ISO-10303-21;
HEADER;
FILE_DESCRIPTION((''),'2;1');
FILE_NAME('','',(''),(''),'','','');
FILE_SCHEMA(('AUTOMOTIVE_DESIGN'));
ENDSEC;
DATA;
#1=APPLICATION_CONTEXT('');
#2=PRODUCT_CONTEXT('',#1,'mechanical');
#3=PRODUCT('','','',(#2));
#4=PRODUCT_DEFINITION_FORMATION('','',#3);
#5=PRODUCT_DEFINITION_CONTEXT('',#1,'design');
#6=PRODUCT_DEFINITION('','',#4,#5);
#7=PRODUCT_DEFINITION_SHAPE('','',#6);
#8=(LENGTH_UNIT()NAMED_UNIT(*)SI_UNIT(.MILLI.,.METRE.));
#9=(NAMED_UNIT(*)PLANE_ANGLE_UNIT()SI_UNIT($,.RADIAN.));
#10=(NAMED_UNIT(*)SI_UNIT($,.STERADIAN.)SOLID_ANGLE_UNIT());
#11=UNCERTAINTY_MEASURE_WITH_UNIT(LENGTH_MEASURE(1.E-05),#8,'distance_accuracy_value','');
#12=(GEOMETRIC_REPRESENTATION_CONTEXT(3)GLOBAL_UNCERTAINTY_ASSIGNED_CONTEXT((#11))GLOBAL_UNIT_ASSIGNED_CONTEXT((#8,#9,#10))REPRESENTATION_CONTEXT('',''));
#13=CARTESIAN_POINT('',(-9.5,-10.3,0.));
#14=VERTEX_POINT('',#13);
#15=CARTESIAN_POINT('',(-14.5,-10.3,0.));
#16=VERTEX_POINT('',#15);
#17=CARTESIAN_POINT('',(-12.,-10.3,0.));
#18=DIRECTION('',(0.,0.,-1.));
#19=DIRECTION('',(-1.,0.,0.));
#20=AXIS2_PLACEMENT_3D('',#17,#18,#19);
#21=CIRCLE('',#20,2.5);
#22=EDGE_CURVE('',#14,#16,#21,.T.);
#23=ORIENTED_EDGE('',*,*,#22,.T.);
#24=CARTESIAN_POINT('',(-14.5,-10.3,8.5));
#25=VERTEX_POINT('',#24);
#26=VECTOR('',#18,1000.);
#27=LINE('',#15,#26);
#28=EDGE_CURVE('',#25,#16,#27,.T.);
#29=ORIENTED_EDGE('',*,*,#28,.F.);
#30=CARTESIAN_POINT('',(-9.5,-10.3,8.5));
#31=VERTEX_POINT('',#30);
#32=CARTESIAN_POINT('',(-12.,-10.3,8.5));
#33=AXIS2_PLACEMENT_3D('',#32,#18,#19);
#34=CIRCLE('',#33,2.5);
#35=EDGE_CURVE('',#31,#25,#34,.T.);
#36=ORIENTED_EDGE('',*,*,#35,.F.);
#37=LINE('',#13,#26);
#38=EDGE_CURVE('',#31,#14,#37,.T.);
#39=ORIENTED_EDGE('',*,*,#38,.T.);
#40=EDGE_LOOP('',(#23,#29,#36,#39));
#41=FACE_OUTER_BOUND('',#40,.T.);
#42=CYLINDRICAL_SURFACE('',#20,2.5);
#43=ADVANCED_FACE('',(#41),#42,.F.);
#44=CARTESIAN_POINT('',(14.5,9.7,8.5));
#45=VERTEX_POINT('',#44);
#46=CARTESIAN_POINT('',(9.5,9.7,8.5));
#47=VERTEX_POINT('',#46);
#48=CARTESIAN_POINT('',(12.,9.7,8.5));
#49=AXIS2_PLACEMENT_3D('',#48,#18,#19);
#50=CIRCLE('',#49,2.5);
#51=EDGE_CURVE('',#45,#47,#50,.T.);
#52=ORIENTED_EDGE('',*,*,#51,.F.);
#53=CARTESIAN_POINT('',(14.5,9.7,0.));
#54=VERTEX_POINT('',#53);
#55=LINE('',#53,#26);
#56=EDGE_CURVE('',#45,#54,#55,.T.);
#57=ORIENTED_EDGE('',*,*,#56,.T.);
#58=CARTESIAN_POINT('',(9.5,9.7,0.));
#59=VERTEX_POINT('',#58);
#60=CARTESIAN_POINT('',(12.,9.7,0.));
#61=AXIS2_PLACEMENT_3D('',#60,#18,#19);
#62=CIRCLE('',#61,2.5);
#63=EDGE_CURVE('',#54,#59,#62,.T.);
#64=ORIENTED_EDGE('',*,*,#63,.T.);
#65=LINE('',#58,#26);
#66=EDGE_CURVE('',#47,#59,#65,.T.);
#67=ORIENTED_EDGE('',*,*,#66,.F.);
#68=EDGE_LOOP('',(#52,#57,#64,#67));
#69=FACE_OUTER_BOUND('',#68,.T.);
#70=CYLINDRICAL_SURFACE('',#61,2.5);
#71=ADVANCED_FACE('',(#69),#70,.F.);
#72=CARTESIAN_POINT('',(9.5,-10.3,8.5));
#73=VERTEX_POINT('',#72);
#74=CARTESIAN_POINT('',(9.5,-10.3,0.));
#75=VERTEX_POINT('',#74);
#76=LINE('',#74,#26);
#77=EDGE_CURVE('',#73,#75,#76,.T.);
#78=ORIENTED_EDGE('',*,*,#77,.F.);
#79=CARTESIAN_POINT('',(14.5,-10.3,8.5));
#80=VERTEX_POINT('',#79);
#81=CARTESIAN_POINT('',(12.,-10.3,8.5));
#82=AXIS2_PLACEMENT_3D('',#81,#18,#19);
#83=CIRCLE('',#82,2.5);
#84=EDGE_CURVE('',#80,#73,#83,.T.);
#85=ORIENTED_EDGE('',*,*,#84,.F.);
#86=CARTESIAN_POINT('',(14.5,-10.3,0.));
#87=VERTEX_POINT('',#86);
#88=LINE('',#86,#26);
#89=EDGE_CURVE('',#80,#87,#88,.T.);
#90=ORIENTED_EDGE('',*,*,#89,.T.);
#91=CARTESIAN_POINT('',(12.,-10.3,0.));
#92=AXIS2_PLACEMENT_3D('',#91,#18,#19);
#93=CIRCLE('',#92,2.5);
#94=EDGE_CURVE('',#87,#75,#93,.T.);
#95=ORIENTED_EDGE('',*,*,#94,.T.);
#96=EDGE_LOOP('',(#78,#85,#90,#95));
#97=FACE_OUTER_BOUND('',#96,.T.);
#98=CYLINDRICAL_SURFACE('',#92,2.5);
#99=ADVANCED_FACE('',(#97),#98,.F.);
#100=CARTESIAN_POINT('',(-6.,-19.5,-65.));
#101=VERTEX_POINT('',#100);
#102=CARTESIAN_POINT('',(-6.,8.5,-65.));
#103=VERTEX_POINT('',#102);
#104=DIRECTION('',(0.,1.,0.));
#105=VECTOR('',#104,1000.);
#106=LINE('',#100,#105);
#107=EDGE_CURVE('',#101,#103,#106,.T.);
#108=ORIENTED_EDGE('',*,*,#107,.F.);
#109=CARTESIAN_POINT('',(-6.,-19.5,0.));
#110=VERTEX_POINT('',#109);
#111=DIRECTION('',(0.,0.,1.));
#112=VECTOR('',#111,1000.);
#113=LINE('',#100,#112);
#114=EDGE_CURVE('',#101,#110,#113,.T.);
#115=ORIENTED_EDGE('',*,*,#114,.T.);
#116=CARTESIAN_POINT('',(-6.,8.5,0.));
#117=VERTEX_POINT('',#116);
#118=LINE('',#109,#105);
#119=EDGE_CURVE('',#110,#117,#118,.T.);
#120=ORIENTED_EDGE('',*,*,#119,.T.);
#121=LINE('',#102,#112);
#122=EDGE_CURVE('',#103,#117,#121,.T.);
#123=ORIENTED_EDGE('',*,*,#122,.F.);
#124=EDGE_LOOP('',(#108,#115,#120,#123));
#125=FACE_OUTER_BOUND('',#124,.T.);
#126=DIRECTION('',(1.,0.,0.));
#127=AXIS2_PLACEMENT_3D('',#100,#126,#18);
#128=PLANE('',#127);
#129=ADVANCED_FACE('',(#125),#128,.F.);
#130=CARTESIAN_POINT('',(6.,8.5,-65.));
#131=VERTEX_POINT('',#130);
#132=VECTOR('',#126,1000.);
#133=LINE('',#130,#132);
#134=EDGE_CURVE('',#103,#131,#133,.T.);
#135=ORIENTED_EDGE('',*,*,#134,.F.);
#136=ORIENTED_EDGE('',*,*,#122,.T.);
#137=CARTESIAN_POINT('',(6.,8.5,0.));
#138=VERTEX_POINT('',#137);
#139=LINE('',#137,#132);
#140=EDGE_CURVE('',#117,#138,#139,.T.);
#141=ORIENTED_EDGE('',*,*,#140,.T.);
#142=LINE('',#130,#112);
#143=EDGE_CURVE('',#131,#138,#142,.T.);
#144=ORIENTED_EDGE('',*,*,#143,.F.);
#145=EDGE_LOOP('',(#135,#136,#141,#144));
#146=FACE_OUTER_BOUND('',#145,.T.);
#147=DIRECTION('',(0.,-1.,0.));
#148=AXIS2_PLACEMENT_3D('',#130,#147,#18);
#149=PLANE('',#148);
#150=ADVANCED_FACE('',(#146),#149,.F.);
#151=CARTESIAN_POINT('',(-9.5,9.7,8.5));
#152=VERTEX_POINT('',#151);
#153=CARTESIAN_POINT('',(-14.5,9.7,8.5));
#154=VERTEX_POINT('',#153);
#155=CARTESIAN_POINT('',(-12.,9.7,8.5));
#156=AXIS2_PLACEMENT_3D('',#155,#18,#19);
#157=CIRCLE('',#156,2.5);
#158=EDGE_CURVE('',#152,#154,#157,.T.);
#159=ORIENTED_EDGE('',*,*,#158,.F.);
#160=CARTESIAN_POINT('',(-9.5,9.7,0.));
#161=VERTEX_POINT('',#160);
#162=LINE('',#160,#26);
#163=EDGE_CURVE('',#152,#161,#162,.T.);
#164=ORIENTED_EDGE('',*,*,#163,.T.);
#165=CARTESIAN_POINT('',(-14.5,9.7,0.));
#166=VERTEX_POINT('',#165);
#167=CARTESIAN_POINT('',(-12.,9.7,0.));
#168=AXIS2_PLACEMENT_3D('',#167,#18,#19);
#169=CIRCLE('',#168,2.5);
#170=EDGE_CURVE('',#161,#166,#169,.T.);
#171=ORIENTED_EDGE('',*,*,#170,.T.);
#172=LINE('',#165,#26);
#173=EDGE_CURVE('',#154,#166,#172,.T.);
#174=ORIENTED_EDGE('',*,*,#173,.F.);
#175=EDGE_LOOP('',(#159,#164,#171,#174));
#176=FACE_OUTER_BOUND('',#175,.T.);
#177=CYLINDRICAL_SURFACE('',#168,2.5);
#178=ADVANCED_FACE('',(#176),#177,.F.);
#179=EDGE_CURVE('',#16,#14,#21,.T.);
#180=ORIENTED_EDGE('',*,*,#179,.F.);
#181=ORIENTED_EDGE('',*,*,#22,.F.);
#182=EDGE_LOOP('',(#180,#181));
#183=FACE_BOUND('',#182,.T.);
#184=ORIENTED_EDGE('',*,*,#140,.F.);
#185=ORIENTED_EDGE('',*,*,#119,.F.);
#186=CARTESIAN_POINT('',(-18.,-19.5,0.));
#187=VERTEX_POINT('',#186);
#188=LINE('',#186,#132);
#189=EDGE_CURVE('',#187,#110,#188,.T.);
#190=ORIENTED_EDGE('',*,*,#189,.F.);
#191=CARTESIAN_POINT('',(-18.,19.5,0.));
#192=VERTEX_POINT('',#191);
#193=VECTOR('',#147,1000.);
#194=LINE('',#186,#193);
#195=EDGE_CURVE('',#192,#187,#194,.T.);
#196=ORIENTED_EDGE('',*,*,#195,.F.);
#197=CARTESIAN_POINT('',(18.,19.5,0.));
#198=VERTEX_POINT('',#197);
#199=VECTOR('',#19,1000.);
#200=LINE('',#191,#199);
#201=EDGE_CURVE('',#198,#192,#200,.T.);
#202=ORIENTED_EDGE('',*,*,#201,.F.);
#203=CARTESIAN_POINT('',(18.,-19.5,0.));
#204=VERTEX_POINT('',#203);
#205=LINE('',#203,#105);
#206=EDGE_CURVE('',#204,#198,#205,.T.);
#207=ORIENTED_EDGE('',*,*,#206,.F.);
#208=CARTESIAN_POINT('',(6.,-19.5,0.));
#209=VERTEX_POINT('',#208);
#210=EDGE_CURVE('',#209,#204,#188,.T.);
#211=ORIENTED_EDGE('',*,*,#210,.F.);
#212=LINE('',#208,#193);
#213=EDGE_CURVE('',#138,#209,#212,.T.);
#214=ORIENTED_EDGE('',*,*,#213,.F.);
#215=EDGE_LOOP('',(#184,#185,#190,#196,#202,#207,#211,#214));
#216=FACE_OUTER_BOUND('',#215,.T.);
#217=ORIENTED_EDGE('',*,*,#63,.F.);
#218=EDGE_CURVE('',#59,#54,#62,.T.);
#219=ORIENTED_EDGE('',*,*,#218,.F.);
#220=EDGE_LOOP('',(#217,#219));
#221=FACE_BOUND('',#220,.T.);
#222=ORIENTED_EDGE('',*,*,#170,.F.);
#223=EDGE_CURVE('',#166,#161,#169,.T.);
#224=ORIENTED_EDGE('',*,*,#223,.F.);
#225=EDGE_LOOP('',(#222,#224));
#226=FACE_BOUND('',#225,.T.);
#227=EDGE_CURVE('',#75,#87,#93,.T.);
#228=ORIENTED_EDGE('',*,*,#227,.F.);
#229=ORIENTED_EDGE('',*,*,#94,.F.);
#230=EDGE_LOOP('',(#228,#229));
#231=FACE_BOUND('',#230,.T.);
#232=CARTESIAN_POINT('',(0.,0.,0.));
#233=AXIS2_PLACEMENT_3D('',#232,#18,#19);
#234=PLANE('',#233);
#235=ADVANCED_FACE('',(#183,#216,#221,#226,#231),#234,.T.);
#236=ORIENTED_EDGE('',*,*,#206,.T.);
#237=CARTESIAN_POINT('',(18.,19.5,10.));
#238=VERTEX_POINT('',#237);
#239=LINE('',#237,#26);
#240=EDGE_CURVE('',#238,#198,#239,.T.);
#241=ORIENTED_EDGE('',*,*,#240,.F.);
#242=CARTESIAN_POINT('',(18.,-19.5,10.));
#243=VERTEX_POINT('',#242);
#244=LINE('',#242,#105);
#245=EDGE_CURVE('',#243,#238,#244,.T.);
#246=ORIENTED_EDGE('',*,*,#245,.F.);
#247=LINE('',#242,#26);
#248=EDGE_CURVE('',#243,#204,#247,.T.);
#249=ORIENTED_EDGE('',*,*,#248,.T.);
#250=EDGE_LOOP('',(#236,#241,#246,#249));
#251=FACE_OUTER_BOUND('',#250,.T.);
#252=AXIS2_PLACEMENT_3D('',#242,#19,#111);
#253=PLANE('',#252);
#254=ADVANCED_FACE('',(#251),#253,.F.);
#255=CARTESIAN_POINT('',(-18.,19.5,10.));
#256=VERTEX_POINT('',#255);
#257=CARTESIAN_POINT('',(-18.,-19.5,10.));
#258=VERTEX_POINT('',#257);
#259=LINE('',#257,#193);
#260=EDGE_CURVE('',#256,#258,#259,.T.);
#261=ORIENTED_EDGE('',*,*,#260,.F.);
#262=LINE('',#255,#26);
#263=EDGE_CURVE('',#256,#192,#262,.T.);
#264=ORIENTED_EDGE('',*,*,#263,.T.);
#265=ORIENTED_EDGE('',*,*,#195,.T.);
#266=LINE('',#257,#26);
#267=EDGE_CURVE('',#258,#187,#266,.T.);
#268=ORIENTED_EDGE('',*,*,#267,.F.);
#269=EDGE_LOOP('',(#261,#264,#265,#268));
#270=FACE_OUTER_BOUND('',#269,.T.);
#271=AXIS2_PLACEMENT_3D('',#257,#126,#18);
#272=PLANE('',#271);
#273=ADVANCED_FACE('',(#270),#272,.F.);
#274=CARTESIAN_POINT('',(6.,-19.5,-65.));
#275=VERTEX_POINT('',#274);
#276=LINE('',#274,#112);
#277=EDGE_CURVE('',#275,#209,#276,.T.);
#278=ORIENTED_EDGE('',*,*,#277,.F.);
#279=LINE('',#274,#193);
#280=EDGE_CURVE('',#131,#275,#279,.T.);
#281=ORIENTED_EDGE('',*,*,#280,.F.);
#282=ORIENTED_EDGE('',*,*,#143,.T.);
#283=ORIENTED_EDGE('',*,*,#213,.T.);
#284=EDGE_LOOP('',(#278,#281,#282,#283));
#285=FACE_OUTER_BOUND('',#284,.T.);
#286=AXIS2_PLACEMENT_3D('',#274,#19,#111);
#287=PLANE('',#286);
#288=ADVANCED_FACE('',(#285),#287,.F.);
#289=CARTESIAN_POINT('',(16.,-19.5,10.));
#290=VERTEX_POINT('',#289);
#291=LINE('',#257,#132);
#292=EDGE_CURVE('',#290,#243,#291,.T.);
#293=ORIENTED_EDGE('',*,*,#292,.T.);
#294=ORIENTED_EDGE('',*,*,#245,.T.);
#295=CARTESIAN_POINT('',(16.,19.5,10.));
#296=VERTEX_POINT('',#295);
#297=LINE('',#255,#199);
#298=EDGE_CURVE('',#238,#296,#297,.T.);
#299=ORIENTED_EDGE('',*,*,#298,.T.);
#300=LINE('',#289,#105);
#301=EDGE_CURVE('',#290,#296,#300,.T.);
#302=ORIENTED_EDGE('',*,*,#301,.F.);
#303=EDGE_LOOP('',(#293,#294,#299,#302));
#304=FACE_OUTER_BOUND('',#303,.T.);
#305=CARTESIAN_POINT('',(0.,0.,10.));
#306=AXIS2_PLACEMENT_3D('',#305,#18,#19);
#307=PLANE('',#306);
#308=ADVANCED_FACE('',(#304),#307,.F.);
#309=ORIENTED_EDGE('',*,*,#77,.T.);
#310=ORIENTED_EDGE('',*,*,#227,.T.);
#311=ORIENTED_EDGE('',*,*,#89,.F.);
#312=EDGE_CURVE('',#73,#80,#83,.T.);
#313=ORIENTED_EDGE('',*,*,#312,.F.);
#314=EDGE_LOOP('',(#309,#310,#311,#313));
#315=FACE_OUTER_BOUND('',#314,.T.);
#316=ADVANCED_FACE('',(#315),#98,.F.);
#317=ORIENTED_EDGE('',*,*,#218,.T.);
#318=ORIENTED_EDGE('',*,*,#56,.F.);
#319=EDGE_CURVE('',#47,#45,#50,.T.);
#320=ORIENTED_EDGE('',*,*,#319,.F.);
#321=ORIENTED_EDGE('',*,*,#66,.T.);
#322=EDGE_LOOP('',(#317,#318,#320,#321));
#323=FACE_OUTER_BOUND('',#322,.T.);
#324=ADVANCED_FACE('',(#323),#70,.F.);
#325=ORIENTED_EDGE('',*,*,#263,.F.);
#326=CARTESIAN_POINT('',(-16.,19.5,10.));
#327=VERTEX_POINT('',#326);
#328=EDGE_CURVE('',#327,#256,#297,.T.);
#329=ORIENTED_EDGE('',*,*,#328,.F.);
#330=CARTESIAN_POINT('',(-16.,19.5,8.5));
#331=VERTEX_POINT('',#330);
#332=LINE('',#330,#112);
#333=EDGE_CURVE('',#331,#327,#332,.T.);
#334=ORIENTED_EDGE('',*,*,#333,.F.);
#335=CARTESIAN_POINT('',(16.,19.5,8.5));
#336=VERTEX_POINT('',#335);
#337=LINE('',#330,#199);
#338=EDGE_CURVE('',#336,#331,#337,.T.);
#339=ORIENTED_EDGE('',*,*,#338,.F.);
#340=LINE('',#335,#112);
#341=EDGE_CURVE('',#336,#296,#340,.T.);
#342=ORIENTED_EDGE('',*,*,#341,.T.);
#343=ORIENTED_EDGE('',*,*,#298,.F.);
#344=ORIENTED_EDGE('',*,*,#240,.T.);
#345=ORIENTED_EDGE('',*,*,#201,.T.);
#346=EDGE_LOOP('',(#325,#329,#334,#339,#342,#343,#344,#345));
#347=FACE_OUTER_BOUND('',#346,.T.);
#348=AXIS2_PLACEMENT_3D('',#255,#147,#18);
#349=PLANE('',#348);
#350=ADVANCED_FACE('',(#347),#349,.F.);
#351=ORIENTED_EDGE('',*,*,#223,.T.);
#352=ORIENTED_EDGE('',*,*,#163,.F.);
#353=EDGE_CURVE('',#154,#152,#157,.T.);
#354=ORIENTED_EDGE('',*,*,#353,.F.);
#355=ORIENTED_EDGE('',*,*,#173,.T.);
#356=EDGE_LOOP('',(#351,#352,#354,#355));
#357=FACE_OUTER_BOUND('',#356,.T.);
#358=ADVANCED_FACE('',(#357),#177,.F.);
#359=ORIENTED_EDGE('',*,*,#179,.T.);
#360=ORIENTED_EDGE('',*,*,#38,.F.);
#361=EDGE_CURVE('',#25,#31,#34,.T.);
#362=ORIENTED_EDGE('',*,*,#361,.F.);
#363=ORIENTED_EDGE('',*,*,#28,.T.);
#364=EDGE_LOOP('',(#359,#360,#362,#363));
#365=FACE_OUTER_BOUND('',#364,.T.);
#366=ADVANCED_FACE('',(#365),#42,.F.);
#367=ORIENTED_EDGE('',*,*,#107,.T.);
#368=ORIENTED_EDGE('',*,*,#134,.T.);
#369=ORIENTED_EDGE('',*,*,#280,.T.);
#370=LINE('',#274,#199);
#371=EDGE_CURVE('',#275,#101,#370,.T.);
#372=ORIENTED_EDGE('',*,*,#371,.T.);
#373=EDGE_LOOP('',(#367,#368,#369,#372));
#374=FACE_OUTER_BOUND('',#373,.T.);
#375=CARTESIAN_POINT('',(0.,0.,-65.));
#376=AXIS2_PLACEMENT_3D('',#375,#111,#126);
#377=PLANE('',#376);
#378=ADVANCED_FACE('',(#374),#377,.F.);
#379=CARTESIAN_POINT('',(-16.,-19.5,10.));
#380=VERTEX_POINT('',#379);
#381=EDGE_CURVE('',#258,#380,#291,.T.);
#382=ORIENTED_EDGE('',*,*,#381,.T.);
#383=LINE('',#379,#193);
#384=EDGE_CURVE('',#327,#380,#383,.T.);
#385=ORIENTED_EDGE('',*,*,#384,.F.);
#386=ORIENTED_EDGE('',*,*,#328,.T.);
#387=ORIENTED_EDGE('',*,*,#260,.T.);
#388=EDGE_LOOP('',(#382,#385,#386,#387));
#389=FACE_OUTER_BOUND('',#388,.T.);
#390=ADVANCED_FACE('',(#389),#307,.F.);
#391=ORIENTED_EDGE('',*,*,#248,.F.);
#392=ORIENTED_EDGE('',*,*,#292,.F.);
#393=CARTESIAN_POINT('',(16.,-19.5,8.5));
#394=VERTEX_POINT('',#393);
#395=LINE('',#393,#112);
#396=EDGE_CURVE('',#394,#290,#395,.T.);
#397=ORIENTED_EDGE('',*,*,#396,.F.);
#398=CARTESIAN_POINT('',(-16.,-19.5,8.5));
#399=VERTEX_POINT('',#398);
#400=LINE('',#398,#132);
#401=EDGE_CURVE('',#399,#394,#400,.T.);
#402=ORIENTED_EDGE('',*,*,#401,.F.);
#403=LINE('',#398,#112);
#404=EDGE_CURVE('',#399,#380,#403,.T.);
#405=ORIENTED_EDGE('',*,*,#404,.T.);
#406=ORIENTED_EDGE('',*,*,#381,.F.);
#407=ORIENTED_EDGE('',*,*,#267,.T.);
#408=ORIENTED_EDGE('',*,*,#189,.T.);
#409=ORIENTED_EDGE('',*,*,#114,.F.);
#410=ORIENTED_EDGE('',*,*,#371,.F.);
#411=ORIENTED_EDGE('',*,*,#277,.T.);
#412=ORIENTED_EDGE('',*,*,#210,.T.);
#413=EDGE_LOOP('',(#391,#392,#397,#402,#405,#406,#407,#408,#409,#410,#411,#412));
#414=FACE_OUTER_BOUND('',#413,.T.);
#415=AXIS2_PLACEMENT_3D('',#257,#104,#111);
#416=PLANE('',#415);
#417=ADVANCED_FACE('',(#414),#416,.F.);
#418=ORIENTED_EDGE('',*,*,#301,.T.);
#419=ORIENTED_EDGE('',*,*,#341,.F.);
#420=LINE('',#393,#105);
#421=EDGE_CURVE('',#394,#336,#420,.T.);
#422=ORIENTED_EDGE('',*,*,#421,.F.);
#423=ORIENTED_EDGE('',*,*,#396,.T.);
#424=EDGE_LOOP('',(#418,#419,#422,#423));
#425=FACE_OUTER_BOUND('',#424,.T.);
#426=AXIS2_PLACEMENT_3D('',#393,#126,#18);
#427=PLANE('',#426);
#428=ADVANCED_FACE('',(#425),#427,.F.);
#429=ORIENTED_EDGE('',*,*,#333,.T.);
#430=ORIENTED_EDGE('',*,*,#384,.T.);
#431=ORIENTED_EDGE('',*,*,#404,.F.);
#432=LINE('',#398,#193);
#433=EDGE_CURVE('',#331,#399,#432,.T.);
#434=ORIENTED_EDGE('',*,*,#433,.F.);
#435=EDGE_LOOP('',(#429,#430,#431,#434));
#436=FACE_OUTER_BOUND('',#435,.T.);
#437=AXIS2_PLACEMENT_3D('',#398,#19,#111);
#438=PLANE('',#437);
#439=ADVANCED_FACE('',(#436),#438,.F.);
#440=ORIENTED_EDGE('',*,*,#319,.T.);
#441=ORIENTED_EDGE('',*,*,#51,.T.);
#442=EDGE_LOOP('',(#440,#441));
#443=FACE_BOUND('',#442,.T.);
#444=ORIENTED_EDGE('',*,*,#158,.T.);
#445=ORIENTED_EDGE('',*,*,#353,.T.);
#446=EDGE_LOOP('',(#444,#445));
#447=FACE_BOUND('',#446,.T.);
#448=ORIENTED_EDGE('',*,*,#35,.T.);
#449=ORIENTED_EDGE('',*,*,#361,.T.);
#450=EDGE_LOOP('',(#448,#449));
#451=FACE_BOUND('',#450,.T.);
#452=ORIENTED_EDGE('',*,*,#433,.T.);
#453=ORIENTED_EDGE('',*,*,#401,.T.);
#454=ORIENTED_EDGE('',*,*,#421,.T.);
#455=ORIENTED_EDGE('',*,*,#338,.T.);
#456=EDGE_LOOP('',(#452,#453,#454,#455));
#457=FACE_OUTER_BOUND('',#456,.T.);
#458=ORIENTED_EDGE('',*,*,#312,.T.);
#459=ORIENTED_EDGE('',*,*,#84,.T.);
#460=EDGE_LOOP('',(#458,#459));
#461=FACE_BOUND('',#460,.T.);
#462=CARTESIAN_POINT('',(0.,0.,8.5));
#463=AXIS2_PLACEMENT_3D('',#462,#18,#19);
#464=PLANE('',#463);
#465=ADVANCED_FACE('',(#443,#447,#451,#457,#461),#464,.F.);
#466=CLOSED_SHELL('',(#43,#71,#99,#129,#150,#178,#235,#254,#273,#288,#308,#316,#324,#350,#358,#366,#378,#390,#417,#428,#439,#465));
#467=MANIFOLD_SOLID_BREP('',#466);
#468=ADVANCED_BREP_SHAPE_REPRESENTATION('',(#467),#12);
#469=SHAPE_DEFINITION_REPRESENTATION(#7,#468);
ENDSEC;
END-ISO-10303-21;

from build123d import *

# Parameters (mm, degrees)
SKETCH_1_W                = 36
SKETCH_1_H                = 39
EXTRUDE_1_DEPTH           = 10
SKETCH_2_W                = 32
SKETCH_2_H                = 39
CUT_EXTRUDE_1_DEPTH       = 1.5
SKETCH_3_W                = 12
SKETCH_3_H                = 28
EXTRUDE_2_DEPTH           = 65
HOLE_WIZARD_5_0_5_1_D     = 5
HOLE_WIZARD_5_0_5_1_DEPTH = 10


with BuildPart() as part:
    # 草图1 → 凸台-拉伸1 (new body)
    with BuildSketch(Plane.XY):
        Rectangle(SKETCH_1_W, SKETCH_1_H)
    extrude(amount=EXTRUDE_1_DEPTH)

    # 草图2 → 切除-拉伸1 (cut)
    with BuildSketch(Plane.XY.offset(10)):
        Rectangle(SKETCH_2_W, SKETCH_2_H)
    extrude(amount=-CUT_EXTRUDE_1_DEPTH, mode=Mode.SUBTRACT)

    # 草图3 → 凸台-拉伸2 (add)
    with BuildSketch(Plane(origin=(0, 0, 0), x_dir=(-1, 0, 0), z_dir=(0, 0, -1))):
        with Locations((0, -5.5)):
            Rectangle(SKETCH_3_W, SKETCH_3_H)
    extrude(amount=EXTRUDE_2_DEPTH)

    # Ø5.0 (5) 直径孔1
    with Locations(Plane(origin=(0, 0, 0), x_dir=(-1, 0, 0), z_dir=(0, 0, -1))):
        with Locations((-12, 9.7), (12, 9.7), (12, -10.3), (-12, -10.3)):
            Hole(HOLE_WIZARD_5_0_5_1_D / 2, depth=HOLE_WIZARD_5_0_5_1_DEPTH)


solid = part.part
